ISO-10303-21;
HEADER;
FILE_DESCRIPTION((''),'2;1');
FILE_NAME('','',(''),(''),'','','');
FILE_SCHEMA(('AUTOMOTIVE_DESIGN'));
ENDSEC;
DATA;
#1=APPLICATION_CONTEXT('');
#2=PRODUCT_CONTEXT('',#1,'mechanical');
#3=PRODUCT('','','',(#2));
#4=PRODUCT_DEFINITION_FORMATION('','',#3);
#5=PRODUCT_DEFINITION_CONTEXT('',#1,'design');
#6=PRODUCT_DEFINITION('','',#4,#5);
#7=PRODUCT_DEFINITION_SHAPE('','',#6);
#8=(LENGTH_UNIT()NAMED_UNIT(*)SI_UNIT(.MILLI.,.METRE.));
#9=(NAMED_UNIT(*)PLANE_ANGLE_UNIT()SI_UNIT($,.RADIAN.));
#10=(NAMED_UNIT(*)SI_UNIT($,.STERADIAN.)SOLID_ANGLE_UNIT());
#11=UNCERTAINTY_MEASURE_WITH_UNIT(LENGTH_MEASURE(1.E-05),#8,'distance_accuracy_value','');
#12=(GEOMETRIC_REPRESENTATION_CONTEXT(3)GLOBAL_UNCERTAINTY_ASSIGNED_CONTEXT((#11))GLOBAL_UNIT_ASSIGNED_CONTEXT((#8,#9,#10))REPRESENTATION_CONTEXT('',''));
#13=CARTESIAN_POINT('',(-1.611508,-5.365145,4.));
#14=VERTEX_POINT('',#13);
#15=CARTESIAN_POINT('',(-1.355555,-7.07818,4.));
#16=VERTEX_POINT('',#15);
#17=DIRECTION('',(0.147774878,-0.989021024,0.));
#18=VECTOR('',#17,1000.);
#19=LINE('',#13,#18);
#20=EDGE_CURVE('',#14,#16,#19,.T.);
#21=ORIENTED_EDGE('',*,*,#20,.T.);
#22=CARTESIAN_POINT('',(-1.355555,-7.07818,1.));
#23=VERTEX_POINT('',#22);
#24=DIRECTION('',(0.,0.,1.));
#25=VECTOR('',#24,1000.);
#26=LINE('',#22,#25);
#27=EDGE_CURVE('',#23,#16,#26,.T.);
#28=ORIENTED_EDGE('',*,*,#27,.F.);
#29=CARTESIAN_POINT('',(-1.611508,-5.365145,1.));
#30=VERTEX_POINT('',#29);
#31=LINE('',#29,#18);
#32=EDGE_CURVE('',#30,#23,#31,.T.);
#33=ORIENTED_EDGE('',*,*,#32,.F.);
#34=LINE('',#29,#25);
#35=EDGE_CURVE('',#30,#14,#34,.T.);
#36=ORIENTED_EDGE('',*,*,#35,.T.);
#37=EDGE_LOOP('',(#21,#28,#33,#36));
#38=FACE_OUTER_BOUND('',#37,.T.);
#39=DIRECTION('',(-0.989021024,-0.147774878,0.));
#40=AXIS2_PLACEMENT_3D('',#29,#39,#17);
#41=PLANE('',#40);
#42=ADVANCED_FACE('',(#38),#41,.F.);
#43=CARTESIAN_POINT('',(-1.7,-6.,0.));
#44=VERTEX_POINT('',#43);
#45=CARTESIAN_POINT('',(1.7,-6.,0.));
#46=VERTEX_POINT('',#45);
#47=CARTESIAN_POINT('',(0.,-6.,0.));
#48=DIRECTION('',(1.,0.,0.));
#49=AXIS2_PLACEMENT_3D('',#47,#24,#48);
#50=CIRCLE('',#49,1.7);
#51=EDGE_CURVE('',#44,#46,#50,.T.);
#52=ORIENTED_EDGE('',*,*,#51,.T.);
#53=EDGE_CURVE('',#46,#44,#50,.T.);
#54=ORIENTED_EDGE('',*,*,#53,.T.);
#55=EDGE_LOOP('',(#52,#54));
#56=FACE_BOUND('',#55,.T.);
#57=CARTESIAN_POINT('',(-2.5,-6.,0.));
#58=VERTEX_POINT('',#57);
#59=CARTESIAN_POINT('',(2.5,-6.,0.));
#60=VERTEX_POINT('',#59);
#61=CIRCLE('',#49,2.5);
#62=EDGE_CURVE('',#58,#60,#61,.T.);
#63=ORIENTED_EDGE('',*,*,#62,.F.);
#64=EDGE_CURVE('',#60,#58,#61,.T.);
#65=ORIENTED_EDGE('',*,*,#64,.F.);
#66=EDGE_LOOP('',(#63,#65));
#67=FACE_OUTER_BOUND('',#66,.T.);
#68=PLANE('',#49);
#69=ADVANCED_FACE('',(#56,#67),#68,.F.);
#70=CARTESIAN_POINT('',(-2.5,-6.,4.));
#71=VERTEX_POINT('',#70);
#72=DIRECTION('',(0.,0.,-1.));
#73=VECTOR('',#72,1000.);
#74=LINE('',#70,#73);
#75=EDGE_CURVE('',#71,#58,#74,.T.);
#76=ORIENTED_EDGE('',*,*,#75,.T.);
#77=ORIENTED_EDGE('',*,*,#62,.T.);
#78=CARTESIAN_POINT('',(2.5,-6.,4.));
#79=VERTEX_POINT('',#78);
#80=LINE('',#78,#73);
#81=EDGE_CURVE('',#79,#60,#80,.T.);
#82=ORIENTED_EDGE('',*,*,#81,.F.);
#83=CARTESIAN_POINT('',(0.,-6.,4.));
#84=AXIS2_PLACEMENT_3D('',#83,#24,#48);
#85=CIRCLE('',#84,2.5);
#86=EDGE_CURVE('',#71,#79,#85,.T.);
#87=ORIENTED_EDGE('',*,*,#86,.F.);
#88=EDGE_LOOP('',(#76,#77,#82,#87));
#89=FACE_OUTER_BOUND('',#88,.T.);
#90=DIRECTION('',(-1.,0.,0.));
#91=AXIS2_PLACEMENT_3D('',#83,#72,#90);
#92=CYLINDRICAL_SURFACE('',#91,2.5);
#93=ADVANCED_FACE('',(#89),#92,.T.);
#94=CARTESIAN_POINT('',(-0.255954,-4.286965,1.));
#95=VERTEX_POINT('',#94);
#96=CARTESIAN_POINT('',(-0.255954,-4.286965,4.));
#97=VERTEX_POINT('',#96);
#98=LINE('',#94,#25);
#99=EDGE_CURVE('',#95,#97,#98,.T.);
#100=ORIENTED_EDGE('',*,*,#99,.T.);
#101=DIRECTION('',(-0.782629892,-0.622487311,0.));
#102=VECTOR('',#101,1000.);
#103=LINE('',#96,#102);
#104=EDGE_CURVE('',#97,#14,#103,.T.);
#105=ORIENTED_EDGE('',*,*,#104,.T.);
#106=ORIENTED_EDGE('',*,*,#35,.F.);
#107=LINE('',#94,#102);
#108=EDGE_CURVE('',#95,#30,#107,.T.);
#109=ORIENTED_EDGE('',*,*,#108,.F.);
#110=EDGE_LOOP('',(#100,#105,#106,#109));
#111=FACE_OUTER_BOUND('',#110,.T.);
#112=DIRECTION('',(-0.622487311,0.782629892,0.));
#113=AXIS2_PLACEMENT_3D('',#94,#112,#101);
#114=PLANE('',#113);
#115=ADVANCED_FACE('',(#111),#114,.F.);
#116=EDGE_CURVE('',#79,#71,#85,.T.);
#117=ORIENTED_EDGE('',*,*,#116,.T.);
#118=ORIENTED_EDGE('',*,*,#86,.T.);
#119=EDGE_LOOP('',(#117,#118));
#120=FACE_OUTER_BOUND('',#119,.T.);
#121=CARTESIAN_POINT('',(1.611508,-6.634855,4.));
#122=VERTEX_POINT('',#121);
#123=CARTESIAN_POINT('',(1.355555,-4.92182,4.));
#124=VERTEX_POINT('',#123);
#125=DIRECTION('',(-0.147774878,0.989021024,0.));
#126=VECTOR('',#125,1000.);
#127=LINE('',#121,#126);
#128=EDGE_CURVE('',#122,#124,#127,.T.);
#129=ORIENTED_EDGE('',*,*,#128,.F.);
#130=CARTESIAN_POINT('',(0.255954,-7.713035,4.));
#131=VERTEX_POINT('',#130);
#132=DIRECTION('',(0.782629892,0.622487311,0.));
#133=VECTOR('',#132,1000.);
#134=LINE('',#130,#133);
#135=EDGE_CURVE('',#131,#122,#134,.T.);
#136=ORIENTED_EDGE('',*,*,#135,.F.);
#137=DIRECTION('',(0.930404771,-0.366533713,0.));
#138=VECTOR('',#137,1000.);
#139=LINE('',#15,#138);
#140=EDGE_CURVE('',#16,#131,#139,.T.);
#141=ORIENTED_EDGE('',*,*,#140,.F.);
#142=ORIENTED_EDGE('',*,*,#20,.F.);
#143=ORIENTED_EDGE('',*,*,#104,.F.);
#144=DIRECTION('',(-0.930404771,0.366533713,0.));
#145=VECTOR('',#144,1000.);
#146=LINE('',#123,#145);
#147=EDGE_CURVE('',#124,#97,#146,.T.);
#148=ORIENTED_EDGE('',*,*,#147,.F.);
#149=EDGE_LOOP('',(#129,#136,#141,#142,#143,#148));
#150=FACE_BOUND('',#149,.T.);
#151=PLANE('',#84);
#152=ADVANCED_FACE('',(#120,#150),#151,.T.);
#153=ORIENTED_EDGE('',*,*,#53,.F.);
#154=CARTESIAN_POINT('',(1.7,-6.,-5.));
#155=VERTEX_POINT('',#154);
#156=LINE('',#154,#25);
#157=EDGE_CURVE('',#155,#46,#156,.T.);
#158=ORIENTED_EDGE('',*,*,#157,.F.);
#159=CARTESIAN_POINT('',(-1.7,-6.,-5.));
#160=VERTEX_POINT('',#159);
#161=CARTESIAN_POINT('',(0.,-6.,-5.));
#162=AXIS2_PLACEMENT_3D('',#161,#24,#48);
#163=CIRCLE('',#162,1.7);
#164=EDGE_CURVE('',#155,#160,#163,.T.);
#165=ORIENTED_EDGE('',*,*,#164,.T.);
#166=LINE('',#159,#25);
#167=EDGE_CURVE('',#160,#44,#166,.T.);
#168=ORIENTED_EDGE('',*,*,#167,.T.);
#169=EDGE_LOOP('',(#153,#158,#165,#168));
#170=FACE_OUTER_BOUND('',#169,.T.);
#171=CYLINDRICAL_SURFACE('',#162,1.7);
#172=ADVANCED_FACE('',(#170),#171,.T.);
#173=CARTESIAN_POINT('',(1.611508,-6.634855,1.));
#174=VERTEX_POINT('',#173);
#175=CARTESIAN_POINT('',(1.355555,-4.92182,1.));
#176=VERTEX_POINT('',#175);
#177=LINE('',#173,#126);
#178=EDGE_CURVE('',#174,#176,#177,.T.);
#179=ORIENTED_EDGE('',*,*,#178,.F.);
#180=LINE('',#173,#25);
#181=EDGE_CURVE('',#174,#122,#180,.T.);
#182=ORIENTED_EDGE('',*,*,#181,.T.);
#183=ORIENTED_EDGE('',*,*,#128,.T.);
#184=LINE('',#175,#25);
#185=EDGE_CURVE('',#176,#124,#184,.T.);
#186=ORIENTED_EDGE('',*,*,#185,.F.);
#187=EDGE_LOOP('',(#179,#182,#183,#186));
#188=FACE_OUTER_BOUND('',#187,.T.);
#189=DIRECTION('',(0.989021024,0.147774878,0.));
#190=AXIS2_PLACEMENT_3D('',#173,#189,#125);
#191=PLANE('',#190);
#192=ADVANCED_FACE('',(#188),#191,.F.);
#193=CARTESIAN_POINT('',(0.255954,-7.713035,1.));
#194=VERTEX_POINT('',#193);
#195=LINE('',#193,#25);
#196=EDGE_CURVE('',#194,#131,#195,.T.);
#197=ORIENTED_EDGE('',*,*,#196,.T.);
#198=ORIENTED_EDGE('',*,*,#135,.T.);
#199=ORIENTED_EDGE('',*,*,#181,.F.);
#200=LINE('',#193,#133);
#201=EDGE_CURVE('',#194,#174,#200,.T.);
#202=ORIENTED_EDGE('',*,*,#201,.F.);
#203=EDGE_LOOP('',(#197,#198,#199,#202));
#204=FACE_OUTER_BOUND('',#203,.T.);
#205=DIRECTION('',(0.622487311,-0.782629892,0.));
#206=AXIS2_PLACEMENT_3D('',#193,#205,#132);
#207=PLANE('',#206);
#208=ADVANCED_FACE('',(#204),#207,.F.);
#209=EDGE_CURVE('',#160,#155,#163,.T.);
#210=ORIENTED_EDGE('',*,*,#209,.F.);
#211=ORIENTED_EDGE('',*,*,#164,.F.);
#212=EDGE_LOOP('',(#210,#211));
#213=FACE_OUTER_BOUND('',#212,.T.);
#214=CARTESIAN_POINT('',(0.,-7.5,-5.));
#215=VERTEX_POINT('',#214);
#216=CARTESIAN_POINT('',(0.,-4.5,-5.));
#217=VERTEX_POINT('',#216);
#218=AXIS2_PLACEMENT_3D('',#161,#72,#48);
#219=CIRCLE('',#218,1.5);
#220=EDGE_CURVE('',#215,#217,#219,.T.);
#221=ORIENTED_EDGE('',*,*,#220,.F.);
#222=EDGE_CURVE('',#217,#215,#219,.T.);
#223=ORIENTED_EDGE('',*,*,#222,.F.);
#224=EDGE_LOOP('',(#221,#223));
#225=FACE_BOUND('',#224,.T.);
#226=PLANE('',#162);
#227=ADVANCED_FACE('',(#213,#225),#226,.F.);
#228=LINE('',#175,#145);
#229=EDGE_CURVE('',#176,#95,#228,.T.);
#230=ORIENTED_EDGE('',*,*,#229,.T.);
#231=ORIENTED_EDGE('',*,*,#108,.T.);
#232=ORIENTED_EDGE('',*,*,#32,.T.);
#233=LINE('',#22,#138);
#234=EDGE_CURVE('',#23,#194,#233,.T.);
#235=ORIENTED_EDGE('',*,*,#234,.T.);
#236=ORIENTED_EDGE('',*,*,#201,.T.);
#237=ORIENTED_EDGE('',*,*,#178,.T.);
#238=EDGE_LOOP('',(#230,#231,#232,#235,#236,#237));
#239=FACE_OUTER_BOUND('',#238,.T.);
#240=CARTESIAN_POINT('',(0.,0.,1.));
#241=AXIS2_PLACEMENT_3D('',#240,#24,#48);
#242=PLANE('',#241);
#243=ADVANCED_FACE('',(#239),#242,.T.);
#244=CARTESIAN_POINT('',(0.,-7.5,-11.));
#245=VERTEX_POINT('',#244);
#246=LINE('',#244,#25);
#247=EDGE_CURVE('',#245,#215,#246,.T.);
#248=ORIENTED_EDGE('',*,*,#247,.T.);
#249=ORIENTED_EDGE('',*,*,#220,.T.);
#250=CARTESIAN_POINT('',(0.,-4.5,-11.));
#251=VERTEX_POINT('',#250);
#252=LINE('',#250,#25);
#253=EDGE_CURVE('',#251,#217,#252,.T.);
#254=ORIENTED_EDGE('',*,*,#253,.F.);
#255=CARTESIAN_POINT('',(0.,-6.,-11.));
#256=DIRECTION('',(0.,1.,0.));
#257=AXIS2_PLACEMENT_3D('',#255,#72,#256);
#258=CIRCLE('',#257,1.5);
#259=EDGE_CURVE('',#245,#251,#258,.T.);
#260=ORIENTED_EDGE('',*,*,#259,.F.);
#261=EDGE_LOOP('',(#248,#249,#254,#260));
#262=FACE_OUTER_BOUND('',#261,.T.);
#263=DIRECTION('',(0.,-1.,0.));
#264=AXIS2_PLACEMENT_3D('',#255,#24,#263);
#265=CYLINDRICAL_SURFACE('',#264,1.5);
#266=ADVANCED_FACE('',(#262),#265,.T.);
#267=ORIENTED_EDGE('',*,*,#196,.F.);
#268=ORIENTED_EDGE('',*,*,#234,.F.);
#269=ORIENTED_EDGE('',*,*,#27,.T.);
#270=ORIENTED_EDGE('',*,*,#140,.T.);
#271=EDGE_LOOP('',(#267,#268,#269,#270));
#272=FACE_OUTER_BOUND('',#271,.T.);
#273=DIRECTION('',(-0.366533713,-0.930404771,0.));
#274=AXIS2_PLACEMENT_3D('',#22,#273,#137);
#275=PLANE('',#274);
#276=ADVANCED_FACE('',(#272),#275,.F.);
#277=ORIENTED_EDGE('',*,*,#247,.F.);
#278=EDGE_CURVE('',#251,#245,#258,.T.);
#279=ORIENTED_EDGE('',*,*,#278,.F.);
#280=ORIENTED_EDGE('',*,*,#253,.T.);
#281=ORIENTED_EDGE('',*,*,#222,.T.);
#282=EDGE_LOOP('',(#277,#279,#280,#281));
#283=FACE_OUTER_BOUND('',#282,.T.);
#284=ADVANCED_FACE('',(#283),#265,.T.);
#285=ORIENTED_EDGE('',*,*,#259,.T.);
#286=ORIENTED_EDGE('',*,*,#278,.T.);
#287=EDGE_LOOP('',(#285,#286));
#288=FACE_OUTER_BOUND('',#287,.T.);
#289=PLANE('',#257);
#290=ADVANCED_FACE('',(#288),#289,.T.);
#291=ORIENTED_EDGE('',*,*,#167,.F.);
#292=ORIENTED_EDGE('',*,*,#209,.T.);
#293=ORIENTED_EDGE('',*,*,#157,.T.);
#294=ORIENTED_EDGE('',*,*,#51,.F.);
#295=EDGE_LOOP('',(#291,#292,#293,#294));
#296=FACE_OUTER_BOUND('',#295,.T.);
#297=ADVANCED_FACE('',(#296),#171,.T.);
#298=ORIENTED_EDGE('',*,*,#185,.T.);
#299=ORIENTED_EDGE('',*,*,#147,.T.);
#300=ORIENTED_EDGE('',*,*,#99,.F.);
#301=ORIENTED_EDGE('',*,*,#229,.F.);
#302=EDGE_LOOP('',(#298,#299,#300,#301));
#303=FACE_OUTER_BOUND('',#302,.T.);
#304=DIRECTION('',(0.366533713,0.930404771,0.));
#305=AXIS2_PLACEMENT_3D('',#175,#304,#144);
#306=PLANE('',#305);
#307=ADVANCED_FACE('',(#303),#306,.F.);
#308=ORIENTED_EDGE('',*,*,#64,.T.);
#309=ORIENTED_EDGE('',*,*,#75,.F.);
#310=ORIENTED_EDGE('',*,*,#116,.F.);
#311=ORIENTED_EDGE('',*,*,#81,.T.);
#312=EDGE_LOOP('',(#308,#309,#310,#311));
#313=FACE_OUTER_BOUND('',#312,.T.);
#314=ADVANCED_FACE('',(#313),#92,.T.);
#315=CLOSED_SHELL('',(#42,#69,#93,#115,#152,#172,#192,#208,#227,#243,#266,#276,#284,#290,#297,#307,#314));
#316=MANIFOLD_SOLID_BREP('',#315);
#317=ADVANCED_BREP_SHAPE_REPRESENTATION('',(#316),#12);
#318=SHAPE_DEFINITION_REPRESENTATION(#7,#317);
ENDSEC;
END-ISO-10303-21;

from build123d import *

# Parameters (mm, degrees)
SKETCH_1_R          = 1.7
EXTRUDE_1_DEPTH     = 5
SKETCH_2_R          = 1.5
EXTRUDE_2_DEPTH     = 6
SKETCH_3_R          = 2.5
EXTRUDE_3_DEPTH     = 4
CUT_EXTRUDE_1_DEPTH = 3


with BuildPart() as part:
    # 草图1 → 凸台-拉伸1 (new body)
    with BuildSketch(Plane.XY):
        with Locations((0, -6)):
            Circle(SKETCH_1_R)
    extrude(amount=-EXTRUDE_1_DEPTH)

    # 草图2 → 凸台-拉伸2 (add)
    with BuildSketch(Plane(origin=(0, 0, -5), x_dir=(-1, 0, 0), z_dir=(0, 0, -1))):
        with Locations(Location((0, -6, 0), (0, 0, 180))):
            Circle(SKETCH_2_R)
    extrude(amount=EXTRUDE_2_DEPTH)

    # 草图3 → 凸台-拉伸3 (add)
    with BuildSketch(Plane.XY):
        with Locations((0, -6)):
            Circle(SKETCH_3_R)
    extrude(amount=EXTRUDE_3_DEPTH)

    # 草图4 → 切除-拉伸1 (cut)
    with BuildSketch(Plane.XY.offset(4)):
        Polygon((1.355554736, -4.921820351), (-0.255953598, -4.286965337), (-1.611508335, -5.365144986), (-1.355554737, -7.078179649), (0.255953597, -7.713034663), (1.611508334, -6.634855014), align=None)
    extrude(amount=-CUT_EXTRUDE_1_DEPTH, mode=Mode.SUBTRACT)


solid = part.part
